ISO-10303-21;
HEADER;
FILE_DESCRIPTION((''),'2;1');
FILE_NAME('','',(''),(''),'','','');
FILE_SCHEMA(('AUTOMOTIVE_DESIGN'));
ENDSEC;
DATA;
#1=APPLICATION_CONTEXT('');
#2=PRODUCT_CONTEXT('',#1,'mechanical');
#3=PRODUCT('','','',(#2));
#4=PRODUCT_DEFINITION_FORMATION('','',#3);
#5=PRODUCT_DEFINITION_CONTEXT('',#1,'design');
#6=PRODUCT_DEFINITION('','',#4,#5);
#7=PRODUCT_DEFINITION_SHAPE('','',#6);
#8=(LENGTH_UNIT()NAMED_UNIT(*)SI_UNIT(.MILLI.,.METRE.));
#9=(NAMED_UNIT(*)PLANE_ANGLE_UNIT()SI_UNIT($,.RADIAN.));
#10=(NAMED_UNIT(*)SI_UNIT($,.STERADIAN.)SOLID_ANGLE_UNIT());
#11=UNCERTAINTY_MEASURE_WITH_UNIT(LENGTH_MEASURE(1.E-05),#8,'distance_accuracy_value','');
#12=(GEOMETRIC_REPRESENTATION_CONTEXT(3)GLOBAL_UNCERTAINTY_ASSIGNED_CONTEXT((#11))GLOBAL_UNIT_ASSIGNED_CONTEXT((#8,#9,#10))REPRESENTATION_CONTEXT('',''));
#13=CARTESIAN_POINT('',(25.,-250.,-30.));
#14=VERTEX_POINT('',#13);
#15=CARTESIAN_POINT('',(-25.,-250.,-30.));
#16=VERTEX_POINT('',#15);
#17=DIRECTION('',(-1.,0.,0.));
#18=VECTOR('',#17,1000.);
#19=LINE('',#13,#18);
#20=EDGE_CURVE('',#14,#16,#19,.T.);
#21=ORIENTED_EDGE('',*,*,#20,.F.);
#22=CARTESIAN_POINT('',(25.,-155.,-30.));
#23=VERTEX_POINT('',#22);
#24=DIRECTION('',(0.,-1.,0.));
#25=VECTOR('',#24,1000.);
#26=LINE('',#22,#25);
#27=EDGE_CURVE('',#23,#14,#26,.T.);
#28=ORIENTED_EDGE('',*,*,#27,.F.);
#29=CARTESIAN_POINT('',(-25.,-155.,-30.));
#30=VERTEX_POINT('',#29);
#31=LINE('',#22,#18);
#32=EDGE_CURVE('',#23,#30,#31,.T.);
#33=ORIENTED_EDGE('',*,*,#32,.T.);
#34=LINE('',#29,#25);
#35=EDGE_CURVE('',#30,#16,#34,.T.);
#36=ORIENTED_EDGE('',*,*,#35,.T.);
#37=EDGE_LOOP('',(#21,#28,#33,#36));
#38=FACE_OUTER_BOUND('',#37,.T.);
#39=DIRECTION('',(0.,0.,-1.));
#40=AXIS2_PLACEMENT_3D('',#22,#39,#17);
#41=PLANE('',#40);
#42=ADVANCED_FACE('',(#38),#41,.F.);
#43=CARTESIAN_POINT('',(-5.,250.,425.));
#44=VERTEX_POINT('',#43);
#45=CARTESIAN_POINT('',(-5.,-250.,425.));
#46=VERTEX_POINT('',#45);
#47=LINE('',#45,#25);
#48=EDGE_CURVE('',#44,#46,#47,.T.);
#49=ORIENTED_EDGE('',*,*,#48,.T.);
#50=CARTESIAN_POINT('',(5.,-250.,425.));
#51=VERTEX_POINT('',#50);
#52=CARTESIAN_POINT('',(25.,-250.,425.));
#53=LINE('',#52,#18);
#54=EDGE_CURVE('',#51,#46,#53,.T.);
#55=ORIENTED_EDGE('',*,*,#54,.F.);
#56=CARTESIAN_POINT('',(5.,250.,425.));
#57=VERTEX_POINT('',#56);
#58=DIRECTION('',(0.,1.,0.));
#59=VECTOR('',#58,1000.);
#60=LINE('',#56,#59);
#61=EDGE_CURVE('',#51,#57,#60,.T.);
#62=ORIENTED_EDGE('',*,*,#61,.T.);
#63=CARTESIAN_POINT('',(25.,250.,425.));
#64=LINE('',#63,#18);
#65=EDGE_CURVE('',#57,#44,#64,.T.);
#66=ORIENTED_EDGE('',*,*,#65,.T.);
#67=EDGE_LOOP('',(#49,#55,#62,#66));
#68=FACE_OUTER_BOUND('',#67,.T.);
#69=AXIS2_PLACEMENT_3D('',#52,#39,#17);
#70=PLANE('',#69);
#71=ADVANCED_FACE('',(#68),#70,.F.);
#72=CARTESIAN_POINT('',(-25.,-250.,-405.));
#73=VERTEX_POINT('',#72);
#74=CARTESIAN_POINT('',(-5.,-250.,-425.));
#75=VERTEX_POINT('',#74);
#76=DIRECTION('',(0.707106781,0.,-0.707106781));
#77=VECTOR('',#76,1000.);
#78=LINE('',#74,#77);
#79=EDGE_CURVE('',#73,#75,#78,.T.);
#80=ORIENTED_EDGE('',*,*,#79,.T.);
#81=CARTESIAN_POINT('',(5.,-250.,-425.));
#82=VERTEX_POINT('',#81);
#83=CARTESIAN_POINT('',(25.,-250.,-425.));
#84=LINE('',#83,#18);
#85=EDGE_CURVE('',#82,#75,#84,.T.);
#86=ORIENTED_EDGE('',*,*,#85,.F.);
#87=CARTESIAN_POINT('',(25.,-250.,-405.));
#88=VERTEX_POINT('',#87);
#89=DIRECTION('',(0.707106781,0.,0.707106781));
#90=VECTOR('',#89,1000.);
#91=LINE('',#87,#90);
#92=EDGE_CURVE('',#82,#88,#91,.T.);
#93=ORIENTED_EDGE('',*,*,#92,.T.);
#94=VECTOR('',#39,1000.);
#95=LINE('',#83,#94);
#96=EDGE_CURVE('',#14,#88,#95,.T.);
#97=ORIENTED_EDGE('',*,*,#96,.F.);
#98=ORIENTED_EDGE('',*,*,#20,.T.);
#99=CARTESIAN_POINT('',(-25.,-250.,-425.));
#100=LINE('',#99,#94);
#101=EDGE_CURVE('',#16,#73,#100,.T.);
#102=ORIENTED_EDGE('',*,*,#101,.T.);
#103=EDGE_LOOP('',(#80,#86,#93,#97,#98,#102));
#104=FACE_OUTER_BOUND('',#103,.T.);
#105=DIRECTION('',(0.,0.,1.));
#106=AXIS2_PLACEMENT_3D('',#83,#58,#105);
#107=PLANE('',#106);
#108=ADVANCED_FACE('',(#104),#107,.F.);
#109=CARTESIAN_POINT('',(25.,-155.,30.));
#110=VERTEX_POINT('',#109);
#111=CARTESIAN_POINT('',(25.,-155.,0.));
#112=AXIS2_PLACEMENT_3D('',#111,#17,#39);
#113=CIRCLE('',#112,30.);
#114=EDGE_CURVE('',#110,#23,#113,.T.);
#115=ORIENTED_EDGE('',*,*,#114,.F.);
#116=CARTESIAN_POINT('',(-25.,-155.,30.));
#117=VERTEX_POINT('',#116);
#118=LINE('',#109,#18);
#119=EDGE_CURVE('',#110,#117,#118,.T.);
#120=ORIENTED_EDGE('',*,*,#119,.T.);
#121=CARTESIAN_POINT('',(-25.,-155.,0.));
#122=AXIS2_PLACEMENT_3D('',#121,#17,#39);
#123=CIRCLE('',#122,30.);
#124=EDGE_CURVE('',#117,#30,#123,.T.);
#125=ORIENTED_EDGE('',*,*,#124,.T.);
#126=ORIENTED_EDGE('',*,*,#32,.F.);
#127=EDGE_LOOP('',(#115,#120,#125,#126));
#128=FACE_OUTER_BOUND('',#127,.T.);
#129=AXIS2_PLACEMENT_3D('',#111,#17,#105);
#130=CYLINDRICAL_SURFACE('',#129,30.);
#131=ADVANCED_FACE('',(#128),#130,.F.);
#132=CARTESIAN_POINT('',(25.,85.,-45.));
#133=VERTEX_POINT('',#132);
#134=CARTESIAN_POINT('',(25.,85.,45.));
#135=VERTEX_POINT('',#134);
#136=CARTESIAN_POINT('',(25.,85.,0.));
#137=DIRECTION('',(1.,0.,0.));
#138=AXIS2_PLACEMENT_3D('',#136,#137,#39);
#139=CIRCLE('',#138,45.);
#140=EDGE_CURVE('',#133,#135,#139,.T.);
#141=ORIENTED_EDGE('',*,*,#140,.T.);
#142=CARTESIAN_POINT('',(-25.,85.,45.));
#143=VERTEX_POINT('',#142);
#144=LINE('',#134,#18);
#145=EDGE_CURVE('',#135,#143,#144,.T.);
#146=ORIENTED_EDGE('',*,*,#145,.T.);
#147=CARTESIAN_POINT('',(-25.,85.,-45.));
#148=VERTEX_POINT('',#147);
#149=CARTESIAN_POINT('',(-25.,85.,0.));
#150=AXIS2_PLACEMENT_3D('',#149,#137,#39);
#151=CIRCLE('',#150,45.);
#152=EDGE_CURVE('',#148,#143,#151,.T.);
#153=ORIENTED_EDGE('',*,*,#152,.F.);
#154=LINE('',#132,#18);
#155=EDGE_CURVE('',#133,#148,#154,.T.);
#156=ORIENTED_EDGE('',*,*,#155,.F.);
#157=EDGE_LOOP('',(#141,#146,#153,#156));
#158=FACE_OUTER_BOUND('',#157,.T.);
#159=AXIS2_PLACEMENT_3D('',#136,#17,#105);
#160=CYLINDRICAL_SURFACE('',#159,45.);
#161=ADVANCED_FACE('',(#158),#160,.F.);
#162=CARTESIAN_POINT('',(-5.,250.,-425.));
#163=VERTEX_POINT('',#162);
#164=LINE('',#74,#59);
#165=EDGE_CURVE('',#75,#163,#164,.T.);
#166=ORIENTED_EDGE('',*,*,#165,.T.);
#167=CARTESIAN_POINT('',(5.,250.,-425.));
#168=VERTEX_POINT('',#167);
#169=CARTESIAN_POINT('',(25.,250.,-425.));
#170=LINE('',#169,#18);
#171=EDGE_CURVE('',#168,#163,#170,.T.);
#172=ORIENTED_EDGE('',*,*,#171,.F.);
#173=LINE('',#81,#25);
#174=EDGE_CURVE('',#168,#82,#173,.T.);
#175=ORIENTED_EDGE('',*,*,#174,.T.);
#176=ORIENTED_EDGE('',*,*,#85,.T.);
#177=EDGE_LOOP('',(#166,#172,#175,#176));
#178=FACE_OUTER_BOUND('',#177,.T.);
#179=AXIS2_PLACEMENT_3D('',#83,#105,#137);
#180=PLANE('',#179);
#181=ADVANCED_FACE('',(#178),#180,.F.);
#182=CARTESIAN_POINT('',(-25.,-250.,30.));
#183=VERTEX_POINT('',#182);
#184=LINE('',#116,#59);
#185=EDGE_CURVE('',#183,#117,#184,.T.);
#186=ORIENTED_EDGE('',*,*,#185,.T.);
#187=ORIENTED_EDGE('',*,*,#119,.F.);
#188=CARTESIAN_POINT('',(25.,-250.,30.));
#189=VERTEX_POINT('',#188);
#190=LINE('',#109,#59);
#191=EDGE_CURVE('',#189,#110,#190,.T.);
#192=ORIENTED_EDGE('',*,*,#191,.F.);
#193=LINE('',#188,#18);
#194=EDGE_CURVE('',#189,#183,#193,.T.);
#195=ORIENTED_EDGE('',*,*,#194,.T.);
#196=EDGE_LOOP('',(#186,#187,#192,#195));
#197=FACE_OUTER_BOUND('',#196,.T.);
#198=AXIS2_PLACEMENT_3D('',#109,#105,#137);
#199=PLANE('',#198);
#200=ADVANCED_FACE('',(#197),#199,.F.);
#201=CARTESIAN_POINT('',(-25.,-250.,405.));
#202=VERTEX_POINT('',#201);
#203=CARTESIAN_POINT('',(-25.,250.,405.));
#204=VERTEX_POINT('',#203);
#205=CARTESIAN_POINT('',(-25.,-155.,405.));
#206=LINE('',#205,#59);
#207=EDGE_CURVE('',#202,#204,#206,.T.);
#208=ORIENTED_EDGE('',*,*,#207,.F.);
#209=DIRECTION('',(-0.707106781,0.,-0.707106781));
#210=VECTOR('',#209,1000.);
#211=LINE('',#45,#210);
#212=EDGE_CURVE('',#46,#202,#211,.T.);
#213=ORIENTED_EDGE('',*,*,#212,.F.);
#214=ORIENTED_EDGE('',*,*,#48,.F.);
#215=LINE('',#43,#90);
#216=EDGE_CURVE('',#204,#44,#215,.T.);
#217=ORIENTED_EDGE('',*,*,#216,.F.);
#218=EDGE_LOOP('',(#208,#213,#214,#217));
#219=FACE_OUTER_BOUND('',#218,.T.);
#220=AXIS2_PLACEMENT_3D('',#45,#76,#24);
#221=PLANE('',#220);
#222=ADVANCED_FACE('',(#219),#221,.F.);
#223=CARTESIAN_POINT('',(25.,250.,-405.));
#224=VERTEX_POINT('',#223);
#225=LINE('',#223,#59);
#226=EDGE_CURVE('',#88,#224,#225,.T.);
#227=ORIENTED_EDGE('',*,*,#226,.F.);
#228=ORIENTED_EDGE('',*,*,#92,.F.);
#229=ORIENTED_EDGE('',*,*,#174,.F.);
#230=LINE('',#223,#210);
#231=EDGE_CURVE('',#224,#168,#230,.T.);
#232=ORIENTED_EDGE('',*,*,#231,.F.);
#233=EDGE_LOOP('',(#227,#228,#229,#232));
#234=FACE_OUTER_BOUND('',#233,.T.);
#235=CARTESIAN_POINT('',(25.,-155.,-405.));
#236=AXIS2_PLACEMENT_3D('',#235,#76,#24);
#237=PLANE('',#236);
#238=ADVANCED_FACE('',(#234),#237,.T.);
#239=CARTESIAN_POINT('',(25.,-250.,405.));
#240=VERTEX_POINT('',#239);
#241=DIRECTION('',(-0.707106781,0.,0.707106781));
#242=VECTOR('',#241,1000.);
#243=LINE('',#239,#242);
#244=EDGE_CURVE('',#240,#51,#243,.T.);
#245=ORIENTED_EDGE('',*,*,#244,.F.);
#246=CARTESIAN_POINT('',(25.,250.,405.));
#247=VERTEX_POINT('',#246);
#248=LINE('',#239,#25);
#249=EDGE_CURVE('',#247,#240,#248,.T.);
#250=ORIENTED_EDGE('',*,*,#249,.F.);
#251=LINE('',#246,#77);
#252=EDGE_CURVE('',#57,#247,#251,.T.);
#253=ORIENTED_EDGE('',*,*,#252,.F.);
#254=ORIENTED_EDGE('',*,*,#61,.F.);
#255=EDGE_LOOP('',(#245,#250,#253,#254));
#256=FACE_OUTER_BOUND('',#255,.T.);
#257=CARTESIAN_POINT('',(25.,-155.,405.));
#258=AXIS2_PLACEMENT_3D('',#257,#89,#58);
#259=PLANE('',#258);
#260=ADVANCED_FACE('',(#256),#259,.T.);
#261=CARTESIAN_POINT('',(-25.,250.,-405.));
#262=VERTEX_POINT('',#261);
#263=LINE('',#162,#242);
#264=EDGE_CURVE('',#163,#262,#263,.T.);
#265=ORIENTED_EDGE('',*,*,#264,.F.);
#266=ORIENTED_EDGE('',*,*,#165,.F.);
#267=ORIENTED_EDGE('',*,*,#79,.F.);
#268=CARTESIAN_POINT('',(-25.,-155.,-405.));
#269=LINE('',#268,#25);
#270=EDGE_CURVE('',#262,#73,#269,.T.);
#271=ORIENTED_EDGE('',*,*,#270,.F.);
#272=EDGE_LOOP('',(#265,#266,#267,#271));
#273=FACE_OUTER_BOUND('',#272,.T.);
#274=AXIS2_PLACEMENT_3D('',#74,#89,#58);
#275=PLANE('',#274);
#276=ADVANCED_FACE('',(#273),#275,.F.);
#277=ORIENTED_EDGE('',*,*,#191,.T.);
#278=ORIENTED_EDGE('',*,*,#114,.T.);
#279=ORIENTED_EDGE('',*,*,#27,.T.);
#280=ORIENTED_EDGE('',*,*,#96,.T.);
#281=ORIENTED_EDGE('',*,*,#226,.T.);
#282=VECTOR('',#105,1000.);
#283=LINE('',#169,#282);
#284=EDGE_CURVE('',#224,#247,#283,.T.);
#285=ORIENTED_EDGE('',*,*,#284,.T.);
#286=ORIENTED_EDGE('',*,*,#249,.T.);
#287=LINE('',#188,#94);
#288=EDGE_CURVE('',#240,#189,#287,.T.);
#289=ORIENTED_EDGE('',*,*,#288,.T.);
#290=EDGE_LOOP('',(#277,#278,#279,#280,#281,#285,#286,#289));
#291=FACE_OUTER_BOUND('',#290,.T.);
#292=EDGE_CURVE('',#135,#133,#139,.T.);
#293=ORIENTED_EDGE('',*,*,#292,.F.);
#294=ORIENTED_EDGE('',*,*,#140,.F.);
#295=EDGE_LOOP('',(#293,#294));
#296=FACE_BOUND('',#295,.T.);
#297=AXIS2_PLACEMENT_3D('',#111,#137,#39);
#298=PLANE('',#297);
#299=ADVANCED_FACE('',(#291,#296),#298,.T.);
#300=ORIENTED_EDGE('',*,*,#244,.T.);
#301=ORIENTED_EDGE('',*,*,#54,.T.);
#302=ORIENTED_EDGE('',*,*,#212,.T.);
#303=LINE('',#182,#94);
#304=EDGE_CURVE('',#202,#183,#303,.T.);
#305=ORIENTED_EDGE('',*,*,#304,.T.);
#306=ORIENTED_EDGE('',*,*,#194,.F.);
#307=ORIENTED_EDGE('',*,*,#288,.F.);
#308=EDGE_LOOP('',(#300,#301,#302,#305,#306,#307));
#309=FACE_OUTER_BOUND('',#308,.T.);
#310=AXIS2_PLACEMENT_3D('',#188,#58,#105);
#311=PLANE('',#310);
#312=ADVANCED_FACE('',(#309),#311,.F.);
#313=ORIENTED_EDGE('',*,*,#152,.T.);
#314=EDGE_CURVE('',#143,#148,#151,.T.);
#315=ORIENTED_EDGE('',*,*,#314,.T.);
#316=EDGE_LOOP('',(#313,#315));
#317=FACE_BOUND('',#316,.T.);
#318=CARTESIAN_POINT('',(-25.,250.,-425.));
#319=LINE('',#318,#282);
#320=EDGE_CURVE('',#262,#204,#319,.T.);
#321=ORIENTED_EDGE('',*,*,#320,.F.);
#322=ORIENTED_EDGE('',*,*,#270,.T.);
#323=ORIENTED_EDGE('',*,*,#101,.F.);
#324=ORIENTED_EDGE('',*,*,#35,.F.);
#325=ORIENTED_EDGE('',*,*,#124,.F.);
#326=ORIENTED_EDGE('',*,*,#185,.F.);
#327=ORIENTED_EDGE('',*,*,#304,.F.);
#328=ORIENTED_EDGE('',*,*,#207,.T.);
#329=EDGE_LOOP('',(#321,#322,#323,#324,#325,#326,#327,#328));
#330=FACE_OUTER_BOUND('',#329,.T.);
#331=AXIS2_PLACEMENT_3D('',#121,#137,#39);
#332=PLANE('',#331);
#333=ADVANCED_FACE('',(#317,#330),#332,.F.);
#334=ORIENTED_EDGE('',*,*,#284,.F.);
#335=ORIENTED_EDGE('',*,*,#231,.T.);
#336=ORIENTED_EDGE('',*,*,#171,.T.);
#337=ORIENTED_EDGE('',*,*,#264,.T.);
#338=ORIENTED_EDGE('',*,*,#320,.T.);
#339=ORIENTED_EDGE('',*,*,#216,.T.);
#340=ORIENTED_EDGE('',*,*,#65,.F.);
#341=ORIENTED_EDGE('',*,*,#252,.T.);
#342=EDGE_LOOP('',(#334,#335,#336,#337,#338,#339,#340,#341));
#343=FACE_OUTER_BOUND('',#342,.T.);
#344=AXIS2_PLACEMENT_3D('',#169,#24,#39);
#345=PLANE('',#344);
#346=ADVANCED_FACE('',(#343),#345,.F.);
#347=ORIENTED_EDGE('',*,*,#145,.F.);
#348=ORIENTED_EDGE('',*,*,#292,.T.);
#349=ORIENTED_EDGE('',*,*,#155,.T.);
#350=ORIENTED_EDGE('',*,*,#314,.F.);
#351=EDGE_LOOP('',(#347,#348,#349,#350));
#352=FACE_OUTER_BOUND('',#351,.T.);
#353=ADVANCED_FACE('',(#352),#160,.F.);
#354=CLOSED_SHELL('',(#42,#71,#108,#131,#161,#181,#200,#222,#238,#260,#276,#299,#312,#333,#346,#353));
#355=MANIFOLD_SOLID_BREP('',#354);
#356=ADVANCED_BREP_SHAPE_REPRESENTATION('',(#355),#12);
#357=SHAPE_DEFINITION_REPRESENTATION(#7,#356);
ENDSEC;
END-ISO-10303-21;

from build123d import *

# Parameters (mm, degrees)
SKETCH1_R           = 45
BOSS_EXTRUDE1_DEPTH = 25
CHAMFER1_SIZE       = 20


with BuildPart() as part:
    # Sketch1 → Boss-Extrude1 (new, symmetric)
    with BuildSketch(Plane(origin=(0, 0, 0), x_dir=(0, 0, -1), z_dir=(1, 0, 0))):
        with BuildLine():
            Line((425, -250), (30, -250))
            Line((30, -250), (30, -155))
            ThreePointArc((30, -155), (0, -125), (-30, -155))
            Line((-30, -155), (-30, -250))
            Line((-30, -250), (-425, -250))
            Line((-425, -250), (-425, 250))
            Line((-425, 250), (425, 250))
            Line((425, 250), (425, -250))
        make_face()
        with Locations((0, 85)):
            Circle(SKETCH1_R, mode=Mode.SUBTRACT)
    extrude(amount=BOSS_EXTRUDE1_DEPTH, both=True)

    # Chamfer1
    chamfer1_edges = [part.edges().sort_by_distance(p)[0] for p in [
        (-25, 0, 425),
        (25, 0, -425),
        (25, 0, 425),
        (-25, 0, -425),
    ]]
    chamfer(chamfer1_edges, length=CHAMFER1_SIZE)


solid = part.part
